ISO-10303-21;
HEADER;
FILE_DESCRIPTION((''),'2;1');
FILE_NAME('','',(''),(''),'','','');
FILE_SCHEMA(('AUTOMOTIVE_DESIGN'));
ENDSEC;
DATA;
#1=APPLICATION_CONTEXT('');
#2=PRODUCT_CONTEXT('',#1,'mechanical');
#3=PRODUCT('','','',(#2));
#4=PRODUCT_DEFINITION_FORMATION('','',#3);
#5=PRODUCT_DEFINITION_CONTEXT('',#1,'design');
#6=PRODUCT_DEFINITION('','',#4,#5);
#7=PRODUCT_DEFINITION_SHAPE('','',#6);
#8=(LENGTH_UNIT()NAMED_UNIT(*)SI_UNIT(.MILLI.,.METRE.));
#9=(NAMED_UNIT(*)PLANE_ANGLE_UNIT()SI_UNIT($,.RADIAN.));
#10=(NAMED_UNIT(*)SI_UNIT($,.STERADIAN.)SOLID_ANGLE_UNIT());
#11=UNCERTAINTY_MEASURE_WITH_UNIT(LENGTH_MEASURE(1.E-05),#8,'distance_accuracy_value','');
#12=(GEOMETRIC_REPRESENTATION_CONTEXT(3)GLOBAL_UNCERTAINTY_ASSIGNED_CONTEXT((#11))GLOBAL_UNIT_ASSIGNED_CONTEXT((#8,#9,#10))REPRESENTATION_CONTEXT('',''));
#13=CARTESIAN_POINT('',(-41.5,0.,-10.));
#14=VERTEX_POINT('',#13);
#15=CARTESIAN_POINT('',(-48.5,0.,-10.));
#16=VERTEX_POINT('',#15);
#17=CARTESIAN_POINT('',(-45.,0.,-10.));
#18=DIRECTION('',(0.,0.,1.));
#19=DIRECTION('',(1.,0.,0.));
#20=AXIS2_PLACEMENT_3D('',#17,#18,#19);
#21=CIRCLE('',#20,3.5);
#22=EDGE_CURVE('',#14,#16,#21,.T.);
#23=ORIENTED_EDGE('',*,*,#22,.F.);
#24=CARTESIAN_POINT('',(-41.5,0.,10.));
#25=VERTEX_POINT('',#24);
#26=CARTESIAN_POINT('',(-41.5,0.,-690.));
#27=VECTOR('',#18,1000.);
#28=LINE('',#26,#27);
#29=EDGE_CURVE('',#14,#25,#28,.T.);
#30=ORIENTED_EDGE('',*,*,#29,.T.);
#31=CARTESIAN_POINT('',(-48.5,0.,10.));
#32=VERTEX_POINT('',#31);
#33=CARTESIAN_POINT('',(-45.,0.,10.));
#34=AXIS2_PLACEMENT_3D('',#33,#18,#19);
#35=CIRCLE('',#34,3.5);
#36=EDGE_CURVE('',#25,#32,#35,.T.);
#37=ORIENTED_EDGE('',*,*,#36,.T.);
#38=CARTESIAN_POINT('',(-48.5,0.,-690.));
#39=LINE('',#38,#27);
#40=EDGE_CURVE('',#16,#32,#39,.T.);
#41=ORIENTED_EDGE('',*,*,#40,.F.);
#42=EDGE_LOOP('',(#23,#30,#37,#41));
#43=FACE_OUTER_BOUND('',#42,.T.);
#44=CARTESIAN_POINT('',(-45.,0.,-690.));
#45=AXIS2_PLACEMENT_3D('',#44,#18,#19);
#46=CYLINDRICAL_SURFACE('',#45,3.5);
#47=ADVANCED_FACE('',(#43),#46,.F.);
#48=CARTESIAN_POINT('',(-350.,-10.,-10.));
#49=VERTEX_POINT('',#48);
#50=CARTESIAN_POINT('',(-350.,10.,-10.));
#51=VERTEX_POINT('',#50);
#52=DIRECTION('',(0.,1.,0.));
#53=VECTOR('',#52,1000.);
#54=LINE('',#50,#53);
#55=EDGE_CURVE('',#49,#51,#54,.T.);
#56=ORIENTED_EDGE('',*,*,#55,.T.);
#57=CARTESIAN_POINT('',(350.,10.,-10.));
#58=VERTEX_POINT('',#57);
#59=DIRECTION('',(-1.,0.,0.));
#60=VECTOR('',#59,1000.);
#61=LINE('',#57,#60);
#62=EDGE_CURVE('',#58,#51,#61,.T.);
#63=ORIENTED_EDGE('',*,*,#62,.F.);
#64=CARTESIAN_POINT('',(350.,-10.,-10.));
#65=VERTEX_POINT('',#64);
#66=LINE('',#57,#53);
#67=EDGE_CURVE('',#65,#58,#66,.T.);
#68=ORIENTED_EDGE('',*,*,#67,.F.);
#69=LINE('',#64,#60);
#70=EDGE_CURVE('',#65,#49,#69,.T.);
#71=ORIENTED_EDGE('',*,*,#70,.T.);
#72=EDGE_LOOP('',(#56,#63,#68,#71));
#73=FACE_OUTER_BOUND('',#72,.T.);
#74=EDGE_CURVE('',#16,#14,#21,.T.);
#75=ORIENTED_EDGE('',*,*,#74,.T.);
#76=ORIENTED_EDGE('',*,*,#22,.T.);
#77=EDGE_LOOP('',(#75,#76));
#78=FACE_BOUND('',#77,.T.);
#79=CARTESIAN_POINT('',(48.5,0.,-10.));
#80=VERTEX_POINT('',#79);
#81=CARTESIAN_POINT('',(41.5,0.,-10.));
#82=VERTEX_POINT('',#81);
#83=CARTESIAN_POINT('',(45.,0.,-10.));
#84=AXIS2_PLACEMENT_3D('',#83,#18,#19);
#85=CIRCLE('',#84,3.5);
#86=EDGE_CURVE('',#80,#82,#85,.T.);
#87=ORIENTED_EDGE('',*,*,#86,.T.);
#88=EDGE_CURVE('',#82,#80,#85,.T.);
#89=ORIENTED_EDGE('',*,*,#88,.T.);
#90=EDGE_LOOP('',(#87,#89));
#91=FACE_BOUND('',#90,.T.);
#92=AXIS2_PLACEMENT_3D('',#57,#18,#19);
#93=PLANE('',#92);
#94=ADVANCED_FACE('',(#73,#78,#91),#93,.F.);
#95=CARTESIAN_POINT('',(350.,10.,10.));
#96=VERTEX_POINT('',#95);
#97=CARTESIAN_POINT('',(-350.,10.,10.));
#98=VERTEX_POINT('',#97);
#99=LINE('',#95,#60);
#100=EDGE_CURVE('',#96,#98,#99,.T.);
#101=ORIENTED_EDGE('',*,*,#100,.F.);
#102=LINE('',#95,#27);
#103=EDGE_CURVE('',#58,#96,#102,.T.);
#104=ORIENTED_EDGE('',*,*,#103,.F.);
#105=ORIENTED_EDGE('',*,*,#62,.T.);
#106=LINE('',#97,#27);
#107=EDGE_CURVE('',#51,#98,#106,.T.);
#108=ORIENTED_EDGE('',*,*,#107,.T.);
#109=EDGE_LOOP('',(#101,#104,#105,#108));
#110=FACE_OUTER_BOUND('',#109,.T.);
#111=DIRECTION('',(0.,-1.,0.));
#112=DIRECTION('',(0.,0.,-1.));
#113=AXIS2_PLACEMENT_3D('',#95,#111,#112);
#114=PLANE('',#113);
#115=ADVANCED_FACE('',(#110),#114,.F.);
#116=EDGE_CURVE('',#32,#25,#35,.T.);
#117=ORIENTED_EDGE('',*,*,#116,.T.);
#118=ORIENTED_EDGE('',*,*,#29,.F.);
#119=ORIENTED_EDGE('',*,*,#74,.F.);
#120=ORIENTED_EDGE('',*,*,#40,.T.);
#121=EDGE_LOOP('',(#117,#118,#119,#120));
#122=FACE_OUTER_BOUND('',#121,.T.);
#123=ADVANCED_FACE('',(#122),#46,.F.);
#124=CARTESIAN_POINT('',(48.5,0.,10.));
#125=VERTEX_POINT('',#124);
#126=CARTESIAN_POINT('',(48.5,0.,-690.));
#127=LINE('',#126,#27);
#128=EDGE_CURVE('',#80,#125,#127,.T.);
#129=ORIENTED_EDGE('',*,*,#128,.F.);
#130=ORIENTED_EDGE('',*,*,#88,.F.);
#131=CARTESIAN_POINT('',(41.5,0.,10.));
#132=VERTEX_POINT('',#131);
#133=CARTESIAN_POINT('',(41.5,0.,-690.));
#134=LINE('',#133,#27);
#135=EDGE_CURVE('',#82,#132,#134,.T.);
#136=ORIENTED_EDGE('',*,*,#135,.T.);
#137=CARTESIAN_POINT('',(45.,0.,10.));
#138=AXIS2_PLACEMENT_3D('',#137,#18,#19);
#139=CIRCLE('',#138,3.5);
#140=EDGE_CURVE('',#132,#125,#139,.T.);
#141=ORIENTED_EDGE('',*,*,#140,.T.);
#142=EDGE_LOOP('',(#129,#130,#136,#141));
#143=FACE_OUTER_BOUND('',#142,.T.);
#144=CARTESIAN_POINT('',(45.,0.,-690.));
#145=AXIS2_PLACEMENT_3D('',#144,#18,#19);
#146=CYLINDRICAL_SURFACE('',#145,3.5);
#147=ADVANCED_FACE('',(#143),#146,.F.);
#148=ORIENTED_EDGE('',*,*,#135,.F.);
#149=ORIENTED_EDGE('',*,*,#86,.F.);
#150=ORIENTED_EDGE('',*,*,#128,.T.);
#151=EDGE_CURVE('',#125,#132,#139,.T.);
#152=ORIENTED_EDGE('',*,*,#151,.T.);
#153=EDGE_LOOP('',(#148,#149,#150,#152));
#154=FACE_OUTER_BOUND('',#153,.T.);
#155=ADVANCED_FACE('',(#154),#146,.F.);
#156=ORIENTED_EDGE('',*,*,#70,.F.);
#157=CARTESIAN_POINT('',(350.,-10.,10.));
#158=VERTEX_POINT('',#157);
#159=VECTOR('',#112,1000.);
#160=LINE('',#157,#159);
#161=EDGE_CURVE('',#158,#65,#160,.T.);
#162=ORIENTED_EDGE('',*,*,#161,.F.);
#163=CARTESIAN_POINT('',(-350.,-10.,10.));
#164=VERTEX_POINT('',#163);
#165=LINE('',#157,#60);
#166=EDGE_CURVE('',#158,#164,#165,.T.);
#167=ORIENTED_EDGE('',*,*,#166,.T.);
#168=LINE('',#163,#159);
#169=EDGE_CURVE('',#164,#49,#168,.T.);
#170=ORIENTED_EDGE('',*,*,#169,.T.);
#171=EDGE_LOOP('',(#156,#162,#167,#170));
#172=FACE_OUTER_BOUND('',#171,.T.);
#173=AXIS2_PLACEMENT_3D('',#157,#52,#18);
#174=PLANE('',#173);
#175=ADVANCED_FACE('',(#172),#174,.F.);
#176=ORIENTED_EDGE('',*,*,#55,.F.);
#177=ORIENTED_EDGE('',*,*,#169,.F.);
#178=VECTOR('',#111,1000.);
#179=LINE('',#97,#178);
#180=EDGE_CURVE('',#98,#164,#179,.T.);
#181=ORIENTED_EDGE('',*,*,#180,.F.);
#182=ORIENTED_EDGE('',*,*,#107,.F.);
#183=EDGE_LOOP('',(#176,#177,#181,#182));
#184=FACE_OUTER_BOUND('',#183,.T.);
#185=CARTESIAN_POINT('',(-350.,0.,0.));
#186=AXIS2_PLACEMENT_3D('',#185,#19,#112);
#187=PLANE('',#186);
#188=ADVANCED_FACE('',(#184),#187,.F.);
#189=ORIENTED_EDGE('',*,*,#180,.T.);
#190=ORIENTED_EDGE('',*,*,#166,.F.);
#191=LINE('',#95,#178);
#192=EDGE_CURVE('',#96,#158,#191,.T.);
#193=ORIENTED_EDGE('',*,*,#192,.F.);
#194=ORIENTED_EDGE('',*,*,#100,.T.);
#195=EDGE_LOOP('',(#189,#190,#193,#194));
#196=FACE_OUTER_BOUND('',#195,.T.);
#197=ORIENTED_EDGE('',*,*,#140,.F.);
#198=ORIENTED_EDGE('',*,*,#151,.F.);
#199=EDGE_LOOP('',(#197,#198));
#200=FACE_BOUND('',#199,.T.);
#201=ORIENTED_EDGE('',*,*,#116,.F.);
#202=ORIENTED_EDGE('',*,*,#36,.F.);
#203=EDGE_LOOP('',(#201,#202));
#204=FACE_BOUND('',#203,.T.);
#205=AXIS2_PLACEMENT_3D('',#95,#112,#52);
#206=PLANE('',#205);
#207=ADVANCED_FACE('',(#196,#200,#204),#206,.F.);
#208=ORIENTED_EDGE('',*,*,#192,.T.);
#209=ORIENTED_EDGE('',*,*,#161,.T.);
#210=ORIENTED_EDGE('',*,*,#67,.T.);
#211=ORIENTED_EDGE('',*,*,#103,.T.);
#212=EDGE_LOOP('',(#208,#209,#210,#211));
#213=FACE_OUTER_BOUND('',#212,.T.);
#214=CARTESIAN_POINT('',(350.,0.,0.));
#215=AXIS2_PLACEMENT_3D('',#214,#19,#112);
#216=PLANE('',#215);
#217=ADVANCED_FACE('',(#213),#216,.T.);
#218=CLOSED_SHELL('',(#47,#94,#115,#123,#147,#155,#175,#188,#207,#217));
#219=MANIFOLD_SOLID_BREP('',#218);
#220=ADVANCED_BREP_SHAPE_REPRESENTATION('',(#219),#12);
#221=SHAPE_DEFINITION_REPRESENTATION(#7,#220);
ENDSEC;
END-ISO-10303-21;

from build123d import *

# Parameters (mm, degrees)
SKETCH_1_W          = 20
SKETCH_1_H          = 20
EXTRUDE_1_DEPTH     = 350
SKETCH_2_R          = 3.5
CUT_EXTRUDE_1_DEPTH = 700


with BuildPart() as part:
    # 草图1 → 凸台-拉伸1 (new, symmetric)
    with BuildSketch(Plane(origin=(0, 0, 0), x_dir=(0, 0, -1), z_dir=(1, 0, 0))):
        Rectangle(SKETCH_1_W, SKETCH_1_H)
    extrude(amount=EXTRUDE_1_DEPTH, both=True)

    # 草图2 → 切除-拉伸1 (cut)
    with BuildSketch(Plane.XY.offset(10)):
        with Locations((-45, 0)):
            Circle(SKETCH_2_R)
        with Locations((45, 0)):
            Circle(SKETCH_2_R)
    extrude(amount=-CUT_EXTRUDE_1_DEPTH, mode=Mode.SUBTRACT)


solid = part.part
